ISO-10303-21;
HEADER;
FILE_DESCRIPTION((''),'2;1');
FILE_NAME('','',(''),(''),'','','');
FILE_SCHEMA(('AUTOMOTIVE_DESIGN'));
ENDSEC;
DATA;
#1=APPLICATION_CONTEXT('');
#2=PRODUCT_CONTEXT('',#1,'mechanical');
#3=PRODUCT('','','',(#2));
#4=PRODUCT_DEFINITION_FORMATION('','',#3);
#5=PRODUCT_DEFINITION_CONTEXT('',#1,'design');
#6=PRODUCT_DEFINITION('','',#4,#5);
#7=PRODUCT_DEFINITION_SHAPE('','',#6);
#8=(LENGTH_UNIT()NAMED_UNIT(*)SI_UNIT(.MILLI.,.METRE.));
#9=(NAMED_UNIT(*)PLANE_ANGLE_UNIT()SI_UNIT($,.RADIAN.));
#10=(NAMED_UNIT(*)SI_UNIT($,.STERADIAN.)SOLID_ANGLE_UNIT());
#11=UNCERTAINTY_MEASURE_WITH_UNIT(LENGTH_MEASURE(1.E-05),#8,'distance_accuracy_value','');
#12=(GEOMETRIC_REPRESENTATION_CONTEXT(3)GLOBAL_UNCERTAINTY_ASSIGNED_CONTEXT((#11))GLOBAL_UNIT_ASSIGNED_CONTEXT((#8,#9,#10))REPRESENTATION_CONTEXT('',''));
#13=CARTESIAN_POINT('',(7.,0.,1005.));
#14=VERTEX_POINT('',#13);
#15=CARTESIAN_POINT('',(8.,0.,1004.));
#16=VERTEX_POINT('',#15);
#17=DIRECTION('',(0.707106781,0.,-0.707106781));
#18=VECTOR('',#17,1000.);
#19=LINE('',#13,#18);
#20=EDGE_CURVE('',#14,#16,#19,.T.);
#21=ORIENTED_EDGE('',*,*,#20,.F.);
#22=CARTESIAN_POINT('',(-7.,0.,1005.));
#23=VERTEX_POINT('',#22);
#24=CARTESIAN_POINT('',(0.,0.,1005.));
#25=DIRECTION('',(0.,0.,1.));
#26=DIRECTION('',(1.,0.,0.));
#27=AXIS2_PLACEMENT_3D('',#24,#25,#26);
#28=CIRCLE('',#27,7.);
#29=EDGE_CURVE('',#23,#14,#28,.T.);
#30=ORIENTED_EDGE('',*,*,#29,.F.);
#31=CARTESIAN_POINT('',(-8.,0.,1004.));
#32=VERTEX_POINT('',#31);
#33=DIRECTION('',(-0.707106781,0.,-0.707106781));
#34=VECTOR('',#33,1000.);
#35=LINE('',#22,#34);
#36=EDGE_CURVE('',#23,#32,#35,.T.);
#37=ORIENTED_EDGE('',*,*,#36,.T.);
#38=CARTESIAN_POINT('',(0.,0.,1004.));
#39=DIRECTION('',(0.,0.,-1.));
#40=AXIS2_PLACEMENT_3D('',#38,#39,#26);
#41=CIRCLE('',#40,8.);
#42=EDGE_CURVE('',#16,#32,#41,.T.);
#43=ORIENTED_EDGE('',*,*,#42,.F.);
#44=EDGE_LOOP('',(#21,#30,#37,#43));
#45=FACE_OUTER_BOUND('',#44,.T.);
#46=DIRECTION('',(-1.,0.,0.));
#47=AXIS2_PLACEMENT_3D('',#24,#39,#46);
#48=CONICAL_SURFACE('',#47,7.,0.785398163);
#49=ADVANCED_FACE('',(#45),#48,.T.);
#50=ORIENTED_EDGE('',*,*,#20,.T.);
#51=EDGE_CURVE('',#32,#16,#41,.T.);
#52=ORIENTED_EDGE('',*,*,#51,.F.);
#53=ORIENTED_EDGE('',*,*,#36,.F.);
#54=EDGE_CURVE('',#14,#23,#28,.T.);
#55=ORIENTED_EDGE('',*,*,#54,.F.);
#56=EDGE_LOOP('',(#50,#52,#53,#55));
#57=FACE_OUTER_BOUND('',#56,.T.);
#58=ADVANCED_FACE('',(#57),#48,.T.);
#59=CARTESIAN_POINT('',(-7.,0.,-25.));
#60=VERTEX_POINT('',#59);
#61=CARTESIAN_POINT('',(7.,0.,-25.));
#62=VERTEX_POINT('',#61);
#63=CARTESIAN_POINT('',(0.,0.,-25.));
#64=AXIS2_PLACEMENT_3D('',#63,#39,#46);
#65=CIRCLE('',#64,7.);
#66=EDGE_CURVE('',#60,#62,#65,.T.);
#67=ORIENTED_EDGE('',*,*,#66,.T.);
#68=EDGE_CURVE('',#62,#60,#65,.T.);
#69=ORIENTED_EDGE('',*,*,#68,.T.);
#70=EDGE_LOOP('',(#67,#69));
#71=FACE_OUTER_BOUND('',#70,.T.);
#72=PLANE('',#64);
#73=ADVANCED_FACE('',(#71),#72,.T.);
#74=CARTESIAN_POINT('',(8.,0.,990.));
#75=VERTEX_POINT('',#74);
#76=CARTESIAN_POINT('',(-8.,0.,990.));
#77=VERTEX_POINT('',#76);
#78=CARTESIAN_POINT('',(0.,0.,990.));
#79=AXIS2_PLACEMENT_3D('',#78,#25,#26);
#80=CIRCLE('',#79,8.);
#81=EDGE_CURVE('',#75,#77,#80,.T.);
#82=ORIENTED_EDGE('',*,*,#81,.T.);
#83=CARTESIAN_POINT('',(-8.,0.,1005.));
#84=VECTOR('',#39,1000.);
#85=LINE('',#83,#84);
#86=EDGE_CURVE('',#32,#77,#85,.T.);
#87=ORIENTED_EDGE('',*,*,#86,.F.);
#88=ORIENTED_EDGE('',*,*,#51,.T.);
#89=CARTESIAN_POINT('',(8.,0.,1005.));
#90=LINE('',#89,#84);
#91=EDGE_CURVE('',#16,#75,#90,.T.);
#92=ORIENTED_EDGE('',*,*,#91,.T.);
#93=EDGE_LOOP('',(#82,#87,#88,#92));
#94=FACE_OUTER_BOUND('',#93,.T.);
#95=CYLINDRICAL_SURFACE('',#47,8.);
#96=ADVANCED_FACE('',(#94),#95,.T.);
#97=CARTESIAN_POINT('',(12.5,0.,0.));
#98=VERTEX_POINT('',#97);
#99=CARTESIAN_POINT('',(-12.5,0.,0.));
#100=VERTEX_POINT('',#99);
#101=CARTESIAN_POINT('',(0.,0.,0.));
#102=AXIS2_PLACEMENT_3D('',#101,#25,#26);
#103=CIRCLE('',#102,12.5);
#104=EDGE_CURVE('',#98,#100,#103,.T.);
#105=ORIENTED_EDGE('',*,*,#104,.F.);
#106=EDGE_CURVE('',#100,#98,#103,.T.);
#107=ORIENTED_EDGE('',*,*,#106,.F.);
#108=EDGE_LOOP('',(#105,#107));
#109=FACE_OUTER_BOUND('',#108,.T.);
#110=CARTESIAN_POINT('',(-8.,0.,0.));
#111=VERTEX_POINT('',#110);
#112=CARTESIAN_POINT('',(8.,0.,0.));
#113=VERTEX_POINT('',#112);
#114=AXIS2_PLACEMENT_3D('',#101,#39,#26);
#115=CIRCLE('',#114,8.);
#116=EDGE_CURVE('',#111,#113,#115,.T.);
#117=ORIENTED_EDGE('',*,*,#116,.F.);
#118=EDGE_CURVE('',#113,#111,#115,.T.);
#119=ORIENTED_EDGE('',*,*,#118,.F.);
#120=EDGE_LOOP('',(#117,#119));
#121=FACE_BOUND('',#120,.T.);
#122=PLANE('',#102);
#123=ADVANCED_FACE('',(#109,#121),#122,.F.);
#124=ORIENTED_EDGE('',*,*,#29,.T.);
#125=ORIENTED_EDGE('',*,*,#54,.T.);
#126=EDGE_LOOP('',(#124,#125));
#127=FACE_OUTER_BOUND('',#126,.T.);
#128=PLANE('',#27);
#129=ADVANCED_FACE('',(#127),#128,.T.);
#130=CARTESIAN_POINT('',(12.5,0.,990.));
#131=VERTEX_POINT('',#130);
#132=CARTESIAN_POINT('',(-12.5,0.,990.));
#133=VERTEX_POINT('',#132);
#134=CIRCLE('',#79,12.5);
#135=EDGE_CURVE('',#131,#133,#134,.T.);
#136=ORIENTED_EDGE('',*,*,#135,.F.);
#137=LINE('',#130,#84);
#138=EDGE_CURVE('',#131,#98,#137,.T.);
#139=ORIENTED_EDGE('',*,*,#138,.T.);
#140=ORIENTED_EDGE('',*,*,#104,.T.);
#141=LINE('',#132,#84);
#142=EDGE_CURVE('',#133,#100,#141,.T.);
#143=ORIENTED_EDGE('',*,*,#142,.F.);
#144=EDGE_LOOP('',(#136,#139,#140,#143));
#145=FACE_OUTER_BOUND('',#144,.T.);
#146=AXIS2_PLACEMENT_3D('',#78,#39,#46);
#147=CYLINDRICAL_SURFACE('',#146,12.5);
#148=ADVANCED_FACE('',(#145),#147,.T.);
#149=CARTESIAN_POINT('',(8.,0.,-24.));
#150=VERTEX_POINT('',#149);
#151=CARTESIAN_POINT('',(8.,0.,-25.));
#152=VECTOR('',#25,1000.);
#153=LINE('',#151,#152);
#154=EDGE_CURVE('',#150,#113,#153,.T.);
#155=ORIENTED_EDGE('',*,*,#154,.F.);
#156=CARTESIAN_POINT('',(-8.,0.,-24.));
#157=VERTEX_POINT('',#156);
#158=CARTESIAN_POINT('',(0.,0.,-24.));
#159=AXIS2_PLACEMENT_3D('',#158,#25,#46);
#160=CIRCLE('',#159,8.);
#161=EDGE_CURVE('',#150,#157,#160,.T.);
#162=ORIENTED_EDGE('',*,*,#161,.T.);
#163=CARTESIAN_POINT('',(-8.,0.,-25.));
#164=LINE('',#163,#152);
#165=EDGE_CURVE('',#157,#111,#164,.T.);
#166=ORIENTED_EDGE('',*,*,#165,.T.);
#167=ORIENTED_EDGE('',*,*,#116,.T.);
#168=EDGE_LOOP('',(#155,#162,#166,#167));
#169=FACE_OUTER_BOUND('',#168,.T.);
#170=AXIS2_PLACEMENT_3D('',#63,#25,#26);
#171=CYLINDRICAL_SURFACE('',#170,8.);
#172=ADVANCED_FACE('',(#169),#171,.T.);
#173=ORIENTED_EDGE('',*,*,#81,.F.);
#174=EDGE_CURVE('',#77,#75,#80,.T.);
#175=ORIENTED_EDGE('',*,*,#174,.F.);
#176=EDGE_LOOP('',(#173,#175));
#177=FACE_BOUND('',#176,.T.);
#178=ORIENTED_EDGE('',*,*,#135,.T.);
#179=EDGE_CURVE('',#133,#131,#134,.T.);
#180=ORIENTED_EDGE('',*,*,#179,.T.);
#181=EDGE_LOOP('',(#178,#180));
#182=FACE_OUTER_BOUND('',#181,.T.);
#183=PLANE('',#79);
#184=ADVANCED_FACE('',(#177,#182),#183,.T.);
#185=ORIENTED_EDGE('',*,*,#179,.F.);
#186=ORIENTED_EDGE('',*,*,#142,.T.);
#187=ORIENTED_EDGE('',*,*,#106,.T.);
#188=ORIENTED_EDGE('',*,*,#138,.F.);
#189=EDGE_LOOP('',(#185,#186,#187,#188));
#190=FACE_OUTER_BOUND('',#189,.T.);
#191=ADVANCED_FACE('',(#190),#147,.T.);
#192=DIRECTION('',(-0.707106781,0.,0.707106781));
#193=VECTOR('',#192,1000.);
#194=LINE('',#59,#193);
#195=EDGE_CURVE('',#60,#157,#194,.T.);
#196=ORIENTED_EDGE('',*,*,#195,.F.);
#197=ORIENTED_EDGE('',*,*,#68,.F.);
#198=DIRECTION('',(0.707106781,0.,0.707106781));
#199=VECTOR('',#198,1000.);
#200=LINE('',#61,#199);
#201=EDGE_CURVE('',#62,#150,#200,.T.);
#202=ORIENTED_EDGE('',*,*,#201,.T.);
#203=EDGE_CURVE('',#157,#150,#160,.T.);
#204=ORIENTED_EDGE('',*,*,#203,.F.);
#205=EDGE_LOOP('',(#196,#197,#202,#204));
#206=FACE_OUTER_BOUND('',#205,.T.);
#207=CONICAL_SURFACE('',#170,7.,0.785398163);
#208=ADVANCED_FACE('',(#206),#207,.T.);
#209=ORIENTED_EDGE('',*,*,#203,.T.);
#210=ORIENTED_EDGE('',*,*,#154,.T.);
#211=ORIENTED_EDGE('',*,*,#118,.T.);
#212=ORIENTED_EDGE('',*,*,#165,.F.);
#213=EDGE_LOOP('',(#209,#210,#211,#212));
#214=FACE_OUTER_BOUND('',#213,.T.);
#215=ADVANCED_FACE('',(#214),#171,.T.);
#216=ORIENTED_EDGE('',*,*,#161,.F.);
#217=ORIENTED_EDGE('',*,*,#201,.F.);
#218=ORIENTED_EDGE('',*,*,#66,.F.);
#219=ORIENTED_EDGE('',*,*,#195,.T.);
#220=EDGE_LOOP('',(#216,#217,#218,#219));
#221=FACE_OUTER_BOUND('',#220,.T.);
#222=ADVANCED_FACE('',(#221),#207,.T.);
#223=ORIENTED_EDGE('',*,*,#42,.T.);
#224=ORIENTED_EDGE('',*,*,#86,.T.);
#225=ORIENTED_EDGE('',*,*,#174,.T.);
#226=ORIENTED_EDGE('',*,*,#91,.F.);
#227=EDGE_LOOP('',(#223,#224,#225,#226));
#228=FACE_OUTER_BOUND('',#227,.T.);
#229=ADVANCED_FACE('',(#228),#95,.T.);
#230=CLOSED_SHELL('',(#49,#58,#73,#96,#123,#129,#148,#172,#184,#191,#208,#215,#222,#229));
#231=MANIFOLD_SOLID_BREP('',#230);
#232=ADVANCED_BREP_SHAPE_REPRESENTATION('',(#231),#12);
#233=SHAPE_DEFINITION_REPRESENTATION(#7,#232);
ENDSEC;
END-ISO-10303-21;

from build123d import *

# Parameters (mm, degrees)
SKETCH_1_R        = 12.5
EXTRUDE_210_DEPTH = 990
SKETCH_2_R        = 8
EXTRUDE_1_DEPTH   = 15
EXTRUDE_START     = 25
SKETCH_3_R        = 8
EXTRUDE_2_DEPTH   = 25
CHAMFER_1_SIZE    = 1


with BuildPart() as part:
    # 草图1 → Extrude 210 (new body)
    with BuildSketch(Plane.XY):
        Circle(SKETCH_1_R)
    extrude(amount=EXTRUDE_210_DEPTH)

    # 草图2 → 凸台-拉伸1 (add)
    with BuildSketch(Plane.XY.offset(990)):
        Circle(SKETCH_2_R)
    extrude(amount=EXTRUDE_1_DEPTH)

    # 草图3 → 凸台-拉伸2 (add)
    with BuildSketch(Plane(origin=(0, 0, 0), x_dir=(-1, 0, 0), z_dir=(0, 0, -1)).offset(EXTRUDE_START)):
        with Locations(Location((0, 0, 0), (0, 0, 180))):
            Circle(SKETCH_3_R)
    extrude(amount=-EXTRUDE_2_DEPTH)

    # 倒角1
    chamfer_1_edges = [part.edges().sort_by_distance(p)[0] for p in [
        (-8, 0, 1005),
        (-8, 0, -25),
    ]]
    chamfer(chamfer_1_edges, length=CHAMFER_1_SIZE)


solid = part.part
